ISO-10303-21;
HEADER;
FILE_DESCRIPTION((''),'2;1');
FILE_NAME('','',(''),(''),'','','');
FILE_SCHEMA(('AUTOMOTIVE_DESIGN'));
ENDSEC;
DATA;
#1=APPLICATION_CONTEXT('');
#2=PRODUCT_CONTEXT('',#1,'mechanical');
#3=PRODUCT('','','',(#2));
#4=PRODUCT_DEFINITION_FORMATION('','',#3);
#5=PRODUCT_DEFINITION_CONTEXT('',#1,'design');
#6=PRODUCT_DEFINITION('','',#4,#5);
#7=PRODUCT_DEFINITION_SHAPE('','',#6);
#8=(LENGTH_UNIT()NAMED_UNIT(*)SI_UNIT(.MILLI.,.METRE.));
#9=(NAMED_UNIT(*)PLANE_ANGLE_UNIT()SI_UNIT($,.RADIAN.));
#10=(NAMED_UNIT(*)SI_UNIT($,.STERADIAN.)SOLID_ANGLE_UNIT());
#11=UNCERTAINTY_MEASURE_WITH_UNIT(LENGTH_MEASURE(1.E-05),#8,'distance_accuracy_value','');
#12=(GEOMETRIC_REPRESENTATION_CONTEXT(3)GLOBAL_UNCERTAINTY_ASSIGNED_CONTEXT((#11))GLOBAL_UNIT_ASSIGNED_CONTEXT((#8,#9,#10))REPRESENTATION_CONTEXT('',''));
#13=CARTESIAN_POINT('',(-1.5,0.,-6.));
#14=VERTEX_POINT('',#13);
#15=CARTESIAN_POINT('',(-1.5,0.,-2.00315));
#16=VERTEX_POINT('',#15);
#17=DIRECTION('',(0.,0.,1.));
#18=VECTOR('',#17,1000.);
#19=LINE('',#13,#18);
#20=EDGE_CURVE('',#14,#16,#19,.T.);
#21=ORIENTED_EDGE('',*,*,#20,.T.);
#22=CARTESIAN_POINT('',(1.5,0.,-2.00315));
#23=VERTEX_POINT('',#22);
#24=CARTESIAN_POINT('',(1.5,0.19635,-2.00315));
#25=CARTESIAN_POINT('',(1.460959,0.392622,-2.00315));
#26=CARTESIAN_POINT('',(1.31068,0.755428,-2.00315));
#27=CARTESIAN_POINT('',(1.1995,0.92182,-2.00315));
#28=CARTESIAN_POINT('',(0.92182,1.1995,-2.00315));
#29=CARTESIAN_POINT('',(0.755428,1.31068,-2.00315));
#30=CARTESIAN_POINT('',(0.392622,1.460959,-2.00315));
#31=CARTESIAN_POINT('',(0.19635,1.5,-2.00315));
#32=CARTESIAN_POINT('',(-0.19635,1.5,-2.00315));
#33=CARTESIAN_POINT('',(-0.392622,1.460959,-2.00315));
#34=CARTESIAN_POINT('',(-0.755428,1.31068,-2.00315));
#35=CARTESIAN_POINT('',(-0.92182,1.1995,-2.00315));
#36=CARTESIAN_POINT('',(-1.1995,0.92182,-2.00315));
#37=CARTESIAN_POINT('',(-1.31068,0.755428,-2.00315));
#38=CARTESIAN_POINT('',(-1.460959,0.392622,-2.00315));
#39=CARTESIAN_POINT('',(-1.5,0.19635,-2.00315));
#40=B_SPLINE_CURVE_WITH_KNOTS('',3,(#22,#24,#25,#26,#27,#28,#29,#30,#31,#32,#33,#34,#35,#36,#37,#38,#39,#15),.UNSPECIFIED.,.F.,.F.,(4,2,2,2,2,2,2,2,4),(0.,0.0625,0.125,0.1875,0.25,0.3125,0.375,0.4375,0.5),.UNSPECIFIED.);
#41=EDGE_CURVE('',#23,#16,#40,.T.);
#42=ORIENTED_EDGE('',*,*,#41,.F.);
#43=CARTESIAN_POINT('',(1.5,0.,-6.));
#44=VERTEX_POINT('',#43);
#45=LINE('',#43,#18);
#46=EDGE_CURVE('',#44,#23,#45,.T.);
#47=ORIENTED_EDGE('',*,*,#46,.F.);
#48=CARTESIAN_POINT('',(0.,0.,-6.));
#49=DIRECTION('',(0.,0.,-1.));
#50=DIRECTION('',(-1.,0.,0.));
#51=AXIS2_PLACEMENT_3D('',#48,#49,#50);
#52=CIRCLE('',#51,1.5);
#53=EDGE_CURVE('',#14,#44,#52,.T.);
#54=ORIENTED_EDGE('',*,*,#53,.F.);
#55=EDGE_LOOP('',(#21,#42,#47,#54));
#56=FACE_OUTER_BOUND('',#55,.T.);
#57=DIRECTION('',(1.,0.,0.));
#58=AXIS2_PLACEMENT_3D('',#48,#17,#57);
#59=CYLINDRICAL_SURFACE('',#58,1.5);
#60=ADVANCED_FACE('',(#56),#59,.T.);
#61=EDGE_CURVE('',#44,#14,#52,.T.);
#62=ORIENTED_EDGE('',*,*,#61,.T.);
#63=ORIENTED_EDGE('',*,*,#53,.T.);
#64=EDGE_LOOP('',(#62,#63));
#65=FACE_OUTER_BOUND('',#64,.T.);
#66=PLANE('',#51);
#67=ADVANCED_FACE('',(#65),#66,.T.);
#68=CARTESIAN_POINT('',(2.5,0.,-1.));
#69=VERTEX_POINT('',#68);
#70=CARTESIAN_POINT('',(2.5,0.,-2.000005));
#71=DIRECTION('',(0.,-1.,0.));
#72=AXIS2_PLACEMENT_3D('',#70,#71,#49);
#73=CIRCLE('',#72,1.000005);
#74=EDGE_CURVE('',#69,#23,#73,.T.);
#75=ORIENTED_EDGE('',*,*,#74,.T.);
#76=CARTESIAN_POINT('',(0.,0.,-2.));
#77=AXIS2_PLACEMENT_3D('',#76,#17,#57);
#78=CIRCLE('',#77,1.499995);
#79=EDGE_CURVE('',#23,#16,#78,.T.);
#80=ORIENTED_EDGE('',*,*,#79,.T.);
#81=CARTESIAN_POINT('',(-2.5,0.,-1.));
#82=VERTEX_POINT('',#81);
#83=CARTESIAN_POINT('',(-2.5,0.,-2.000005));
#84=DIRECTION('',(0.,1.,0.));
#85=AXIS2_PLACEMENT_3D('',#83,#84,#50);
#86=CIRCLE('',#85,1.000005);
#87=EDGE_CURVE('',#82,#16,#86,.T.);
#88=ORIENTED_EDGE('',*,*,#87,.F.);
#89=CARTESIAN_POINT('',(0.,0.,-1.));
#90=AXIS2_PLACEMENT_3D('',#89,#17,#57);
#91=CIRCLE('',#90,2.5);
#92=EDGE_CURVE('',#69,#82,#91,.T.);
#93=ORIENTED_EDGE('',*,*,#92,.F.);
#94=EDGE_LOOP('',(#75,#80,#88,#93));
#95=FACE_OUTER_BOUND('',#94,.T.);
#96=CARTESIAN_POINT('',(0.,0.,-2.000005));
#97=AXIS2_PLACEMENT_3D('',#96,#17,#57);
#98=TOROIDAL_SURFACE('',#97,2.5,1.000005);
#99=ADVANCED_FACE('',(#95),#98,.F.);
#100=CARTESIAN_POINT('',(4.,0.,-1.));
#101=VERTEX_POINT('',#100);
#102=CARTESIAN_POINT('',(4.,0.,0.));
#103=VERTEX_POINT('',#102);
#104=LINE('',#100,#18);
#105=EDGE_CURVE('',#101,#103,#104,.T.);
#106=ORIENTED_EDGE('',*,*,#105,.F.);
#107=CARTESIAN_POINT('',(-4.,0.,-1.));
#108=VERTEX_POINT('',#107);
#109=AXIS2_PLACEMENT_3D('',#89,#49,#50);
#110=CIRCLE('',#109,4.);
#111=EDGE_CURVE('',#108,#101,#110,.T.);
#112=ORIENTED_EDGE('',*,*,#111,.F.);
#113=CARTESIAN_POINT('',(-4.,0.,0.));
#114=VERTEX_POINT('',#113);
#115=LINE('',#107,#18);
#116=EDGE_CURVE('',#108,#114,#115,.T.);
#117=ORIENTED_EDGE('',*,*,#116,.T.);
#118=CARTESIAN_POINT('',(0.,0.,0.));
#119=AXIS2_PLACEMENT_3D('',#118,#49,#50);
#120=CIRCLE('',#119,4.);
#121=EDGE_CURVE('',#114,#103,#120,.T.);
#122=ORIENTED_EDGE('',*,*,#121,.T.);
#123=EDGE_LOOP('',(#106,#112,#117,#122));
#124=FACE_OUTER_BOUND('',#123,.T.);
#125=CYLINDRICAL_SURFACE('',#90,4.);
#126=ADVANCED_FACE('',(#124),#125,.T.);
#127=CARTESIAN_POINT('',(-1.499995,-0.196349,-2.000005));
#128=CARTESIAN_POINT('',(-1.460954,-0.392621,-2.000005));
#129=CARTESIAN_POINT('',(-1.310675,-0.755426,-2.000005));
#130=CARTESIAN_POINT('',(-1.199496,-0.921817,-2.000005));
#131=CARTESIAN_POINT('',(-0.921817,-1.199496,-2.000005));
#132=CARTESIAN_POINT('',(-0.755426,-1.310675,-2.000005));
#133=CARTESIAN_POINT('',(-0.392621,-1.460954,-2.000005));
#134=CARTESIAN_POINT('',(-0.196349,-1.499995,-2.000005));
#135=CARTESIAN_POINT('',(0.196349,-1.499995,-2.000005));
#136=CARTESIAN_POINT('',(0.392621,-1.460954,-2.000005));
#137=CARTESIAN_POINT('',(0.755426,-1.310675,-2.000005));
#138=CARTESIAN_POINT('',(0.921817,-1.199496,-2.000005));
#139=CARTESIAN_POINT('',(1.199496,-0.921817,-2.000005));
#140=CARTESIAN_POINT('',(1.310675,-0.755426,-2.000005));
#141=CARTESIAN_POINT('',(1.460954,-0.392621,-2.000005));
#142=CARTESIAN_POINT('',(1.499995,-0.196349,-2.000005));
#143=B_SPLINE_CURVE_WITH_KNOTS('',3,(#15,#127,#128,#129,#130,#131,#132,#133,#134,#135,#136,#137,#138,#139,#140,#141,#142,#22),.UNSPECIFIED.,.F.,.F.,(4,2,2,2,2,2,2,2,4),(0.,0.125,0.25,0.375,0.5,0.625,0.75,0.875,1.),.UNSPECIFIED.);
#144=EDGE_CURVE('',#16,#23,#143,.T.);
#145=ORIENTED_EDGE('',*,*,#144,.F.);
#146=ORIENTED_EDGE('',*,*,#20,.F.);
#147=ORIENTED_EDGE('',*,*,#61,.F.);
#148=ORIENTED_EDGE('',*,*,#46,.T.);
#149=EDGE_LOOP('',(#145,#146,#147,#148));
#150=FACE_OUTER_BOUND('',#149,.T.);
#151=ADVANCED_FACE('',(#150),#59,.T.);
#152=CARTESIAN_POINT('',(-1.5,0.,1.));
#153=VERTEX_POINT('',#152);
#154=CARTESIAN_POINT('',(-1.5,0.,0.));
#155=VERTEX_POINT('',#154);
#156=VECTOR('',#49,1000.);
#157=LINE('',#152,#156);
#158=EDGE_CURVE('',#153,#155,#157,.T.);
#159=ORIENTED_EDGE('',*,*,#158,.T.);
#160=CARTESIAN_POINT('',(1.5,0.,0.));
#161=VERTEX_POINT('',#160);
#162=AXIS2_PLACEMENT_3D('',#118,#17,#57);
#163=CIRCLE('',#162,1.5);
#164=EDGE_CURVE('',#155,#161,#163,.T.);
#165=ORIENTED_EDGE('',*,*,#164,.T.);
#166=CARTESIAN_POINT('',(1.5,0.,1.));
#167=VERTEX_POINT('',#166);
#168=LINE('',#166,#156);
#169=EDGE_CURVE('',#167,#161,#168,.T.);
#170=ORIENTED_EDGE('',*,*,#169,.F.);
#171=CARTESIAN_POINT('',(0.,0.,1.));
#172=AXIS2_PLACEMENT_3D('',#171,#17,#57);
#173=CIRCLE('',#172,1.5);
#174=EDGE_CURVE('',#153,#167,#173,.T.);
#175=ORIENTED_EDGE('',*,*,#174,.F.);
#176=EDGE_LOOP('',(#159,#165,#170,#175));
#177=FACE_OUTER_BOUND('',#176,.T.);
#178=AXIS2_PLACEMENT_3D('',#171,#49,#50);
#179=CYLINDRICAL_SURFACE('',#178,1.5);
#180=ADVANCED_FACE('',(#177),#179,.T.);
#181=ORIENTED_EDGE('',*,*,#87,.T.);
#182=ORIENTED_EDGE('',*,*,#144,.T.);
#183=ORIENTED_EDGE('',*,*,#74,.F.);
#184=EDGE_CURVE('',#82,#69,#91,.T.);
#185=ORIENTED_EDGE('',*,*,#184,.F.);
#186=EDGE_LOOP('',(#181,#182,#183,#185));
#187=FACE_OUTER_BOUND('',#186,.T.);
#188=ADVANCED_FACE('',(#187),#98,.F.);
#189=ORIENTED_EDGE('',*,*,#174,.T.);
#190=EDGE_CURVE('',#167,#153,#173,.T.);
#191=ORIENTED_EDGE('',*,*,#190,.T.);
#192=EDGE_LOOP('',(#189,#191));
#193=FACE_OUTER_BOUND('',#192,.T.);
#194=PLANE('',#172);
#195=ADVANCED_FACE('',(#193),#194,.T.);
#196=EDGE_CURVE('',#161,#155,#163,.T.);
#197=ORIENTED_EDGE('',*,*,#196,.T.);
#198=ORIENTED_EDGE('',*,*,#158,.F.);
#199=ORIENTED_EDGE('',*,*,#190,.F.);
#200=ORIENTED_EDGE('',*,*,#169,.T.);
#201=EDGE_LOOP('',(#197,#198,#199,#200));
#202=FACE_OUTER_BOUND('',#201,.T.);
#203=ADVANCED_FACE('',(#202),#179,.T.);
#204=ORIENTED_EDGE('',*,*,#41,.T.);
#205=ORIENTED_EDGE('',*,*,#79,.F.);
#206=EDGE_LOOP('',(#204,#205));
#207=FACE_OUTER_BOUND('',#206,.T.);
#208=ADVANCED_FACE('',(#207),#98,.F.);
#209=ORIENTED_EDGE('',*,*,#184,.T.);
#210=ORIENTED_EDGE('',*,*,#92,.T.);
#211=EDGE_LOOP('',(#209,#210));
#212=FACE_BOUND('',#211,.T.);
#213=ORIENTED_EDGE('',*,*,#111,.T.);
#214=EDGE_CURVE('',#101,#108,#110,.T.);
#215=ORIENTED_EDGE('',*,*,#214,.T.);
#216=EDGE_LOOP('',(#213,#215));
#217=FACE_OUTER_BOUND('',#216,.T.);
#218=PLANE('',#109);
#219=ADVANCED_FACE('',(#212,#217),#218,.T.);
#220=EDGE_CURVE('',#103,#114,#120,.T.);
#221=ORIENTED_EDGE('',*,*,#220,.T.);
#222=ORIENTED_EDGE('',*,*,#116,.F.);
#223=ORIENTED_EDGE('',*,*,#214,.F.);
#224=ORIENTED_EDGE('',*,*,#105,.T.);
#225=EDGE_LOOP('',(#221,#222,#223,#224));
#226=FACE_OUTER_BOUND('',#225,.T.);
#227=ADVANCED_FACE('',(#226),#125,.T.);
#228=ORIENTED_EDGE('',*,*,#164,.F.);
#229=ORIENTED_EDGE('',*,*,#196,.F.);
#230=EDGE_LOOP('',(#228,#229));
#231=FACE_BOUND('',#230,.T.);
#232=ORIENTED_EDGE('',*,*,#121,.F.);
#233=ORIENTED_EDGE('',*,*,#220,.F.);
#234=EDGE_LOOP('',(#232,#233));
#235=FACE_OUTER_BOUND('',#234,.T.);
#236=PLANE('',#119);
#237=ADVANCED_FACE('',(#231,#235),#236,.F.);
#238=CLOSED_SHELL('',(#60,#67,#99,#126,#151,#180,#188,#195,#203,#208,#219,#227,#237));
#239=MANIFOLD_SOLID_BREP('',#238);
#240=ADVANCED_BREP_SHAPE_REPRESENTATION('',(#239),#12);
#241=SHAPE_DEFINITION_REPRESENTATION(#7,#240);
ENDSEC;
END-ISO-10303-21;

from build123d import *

# Parameters (mm, degrees)
SKETCH_1_R           = 1.5
BOSS_EXTRUDE_1_DEPTH = 1
SKETCH_2_R           = 4
BOSS_EXTRUDE_2_DEPTH = 1
SKETCH_3_R           = 2.5
BOSS_EXTRUDE_3_DEPTH = 1
BOSS_EXTRUDE_START   = 4
SKETCH_4_R           = 1.5
BOSS_EXTRUDE_4_DEPTH = 4


with BuildPart() as part:
    # Sketch 1 → Boss-Extrude 1 (new body)
    with BuildSketch(Plane.XY):
        Circle(SKETCH_1_R)
    extrude(amount=BOSS_EXTRUDE_1_DEPTH)

    # Sketch 2 → Boss-Extrude 2 (add)
    with BuildSketch(Plane(origin=(0, 0, 0), x_dir=(-1, 0, 0), z_dir=(0, 0, -1))):
        Circle(SKETCH_2_R)
    extrude(amount=BOSS_EXTRUDE_2_DEPTH)

    # Sketch 3 → Boss-Extrude 3 (add)
    with BuildSketch(Plane(origin=(0, 0, -1), x_dir=(-1, 0, 0), z_dir=(0, 0, -1))):
        Circle(SKETCH_3_R)
    extrude(amount=BOSS_EXTRUDE_3_DEPTH)

    # Sketch 4 → Boss-Extrude 4 (add)
    with BuildSketch(Plane(origin=(0, 0, -2), x_dir=(-1, 0, 0), z_dir=(0, 0, -1)).offset(BOSS_EXTRUDE_START)):
        with Locations(Location((0, 0, 0), (0, 0, 180))):
            Circle(SKETCH_4_R)
    extrude(amount=-BOSS_EXTRUDE_4_DEPTH)

    # Sketch 5 → Cut-Revolve 2 (revolve, cut)
    with BuildSketch(Plane(origin=(0, 0, 0), x_dir=(1, 0, 0), z_dir=(0, 1, 0))):
        with BuildLine():
            Line((1.5, 2.003149648), (2.5, 2.000004945))
            Line((2.5, 2.000004945), (2.5, 1))
            ThreePointArc((2.5, 1), (1.791778774, 1.294007363), (1.5, 2.003149648))
        make_face()
    revolve(axis=Axis((0, 0, -2.003149648), (0, 0, -1)), mode=Mode.SUBTRACT)


solid = part.part
